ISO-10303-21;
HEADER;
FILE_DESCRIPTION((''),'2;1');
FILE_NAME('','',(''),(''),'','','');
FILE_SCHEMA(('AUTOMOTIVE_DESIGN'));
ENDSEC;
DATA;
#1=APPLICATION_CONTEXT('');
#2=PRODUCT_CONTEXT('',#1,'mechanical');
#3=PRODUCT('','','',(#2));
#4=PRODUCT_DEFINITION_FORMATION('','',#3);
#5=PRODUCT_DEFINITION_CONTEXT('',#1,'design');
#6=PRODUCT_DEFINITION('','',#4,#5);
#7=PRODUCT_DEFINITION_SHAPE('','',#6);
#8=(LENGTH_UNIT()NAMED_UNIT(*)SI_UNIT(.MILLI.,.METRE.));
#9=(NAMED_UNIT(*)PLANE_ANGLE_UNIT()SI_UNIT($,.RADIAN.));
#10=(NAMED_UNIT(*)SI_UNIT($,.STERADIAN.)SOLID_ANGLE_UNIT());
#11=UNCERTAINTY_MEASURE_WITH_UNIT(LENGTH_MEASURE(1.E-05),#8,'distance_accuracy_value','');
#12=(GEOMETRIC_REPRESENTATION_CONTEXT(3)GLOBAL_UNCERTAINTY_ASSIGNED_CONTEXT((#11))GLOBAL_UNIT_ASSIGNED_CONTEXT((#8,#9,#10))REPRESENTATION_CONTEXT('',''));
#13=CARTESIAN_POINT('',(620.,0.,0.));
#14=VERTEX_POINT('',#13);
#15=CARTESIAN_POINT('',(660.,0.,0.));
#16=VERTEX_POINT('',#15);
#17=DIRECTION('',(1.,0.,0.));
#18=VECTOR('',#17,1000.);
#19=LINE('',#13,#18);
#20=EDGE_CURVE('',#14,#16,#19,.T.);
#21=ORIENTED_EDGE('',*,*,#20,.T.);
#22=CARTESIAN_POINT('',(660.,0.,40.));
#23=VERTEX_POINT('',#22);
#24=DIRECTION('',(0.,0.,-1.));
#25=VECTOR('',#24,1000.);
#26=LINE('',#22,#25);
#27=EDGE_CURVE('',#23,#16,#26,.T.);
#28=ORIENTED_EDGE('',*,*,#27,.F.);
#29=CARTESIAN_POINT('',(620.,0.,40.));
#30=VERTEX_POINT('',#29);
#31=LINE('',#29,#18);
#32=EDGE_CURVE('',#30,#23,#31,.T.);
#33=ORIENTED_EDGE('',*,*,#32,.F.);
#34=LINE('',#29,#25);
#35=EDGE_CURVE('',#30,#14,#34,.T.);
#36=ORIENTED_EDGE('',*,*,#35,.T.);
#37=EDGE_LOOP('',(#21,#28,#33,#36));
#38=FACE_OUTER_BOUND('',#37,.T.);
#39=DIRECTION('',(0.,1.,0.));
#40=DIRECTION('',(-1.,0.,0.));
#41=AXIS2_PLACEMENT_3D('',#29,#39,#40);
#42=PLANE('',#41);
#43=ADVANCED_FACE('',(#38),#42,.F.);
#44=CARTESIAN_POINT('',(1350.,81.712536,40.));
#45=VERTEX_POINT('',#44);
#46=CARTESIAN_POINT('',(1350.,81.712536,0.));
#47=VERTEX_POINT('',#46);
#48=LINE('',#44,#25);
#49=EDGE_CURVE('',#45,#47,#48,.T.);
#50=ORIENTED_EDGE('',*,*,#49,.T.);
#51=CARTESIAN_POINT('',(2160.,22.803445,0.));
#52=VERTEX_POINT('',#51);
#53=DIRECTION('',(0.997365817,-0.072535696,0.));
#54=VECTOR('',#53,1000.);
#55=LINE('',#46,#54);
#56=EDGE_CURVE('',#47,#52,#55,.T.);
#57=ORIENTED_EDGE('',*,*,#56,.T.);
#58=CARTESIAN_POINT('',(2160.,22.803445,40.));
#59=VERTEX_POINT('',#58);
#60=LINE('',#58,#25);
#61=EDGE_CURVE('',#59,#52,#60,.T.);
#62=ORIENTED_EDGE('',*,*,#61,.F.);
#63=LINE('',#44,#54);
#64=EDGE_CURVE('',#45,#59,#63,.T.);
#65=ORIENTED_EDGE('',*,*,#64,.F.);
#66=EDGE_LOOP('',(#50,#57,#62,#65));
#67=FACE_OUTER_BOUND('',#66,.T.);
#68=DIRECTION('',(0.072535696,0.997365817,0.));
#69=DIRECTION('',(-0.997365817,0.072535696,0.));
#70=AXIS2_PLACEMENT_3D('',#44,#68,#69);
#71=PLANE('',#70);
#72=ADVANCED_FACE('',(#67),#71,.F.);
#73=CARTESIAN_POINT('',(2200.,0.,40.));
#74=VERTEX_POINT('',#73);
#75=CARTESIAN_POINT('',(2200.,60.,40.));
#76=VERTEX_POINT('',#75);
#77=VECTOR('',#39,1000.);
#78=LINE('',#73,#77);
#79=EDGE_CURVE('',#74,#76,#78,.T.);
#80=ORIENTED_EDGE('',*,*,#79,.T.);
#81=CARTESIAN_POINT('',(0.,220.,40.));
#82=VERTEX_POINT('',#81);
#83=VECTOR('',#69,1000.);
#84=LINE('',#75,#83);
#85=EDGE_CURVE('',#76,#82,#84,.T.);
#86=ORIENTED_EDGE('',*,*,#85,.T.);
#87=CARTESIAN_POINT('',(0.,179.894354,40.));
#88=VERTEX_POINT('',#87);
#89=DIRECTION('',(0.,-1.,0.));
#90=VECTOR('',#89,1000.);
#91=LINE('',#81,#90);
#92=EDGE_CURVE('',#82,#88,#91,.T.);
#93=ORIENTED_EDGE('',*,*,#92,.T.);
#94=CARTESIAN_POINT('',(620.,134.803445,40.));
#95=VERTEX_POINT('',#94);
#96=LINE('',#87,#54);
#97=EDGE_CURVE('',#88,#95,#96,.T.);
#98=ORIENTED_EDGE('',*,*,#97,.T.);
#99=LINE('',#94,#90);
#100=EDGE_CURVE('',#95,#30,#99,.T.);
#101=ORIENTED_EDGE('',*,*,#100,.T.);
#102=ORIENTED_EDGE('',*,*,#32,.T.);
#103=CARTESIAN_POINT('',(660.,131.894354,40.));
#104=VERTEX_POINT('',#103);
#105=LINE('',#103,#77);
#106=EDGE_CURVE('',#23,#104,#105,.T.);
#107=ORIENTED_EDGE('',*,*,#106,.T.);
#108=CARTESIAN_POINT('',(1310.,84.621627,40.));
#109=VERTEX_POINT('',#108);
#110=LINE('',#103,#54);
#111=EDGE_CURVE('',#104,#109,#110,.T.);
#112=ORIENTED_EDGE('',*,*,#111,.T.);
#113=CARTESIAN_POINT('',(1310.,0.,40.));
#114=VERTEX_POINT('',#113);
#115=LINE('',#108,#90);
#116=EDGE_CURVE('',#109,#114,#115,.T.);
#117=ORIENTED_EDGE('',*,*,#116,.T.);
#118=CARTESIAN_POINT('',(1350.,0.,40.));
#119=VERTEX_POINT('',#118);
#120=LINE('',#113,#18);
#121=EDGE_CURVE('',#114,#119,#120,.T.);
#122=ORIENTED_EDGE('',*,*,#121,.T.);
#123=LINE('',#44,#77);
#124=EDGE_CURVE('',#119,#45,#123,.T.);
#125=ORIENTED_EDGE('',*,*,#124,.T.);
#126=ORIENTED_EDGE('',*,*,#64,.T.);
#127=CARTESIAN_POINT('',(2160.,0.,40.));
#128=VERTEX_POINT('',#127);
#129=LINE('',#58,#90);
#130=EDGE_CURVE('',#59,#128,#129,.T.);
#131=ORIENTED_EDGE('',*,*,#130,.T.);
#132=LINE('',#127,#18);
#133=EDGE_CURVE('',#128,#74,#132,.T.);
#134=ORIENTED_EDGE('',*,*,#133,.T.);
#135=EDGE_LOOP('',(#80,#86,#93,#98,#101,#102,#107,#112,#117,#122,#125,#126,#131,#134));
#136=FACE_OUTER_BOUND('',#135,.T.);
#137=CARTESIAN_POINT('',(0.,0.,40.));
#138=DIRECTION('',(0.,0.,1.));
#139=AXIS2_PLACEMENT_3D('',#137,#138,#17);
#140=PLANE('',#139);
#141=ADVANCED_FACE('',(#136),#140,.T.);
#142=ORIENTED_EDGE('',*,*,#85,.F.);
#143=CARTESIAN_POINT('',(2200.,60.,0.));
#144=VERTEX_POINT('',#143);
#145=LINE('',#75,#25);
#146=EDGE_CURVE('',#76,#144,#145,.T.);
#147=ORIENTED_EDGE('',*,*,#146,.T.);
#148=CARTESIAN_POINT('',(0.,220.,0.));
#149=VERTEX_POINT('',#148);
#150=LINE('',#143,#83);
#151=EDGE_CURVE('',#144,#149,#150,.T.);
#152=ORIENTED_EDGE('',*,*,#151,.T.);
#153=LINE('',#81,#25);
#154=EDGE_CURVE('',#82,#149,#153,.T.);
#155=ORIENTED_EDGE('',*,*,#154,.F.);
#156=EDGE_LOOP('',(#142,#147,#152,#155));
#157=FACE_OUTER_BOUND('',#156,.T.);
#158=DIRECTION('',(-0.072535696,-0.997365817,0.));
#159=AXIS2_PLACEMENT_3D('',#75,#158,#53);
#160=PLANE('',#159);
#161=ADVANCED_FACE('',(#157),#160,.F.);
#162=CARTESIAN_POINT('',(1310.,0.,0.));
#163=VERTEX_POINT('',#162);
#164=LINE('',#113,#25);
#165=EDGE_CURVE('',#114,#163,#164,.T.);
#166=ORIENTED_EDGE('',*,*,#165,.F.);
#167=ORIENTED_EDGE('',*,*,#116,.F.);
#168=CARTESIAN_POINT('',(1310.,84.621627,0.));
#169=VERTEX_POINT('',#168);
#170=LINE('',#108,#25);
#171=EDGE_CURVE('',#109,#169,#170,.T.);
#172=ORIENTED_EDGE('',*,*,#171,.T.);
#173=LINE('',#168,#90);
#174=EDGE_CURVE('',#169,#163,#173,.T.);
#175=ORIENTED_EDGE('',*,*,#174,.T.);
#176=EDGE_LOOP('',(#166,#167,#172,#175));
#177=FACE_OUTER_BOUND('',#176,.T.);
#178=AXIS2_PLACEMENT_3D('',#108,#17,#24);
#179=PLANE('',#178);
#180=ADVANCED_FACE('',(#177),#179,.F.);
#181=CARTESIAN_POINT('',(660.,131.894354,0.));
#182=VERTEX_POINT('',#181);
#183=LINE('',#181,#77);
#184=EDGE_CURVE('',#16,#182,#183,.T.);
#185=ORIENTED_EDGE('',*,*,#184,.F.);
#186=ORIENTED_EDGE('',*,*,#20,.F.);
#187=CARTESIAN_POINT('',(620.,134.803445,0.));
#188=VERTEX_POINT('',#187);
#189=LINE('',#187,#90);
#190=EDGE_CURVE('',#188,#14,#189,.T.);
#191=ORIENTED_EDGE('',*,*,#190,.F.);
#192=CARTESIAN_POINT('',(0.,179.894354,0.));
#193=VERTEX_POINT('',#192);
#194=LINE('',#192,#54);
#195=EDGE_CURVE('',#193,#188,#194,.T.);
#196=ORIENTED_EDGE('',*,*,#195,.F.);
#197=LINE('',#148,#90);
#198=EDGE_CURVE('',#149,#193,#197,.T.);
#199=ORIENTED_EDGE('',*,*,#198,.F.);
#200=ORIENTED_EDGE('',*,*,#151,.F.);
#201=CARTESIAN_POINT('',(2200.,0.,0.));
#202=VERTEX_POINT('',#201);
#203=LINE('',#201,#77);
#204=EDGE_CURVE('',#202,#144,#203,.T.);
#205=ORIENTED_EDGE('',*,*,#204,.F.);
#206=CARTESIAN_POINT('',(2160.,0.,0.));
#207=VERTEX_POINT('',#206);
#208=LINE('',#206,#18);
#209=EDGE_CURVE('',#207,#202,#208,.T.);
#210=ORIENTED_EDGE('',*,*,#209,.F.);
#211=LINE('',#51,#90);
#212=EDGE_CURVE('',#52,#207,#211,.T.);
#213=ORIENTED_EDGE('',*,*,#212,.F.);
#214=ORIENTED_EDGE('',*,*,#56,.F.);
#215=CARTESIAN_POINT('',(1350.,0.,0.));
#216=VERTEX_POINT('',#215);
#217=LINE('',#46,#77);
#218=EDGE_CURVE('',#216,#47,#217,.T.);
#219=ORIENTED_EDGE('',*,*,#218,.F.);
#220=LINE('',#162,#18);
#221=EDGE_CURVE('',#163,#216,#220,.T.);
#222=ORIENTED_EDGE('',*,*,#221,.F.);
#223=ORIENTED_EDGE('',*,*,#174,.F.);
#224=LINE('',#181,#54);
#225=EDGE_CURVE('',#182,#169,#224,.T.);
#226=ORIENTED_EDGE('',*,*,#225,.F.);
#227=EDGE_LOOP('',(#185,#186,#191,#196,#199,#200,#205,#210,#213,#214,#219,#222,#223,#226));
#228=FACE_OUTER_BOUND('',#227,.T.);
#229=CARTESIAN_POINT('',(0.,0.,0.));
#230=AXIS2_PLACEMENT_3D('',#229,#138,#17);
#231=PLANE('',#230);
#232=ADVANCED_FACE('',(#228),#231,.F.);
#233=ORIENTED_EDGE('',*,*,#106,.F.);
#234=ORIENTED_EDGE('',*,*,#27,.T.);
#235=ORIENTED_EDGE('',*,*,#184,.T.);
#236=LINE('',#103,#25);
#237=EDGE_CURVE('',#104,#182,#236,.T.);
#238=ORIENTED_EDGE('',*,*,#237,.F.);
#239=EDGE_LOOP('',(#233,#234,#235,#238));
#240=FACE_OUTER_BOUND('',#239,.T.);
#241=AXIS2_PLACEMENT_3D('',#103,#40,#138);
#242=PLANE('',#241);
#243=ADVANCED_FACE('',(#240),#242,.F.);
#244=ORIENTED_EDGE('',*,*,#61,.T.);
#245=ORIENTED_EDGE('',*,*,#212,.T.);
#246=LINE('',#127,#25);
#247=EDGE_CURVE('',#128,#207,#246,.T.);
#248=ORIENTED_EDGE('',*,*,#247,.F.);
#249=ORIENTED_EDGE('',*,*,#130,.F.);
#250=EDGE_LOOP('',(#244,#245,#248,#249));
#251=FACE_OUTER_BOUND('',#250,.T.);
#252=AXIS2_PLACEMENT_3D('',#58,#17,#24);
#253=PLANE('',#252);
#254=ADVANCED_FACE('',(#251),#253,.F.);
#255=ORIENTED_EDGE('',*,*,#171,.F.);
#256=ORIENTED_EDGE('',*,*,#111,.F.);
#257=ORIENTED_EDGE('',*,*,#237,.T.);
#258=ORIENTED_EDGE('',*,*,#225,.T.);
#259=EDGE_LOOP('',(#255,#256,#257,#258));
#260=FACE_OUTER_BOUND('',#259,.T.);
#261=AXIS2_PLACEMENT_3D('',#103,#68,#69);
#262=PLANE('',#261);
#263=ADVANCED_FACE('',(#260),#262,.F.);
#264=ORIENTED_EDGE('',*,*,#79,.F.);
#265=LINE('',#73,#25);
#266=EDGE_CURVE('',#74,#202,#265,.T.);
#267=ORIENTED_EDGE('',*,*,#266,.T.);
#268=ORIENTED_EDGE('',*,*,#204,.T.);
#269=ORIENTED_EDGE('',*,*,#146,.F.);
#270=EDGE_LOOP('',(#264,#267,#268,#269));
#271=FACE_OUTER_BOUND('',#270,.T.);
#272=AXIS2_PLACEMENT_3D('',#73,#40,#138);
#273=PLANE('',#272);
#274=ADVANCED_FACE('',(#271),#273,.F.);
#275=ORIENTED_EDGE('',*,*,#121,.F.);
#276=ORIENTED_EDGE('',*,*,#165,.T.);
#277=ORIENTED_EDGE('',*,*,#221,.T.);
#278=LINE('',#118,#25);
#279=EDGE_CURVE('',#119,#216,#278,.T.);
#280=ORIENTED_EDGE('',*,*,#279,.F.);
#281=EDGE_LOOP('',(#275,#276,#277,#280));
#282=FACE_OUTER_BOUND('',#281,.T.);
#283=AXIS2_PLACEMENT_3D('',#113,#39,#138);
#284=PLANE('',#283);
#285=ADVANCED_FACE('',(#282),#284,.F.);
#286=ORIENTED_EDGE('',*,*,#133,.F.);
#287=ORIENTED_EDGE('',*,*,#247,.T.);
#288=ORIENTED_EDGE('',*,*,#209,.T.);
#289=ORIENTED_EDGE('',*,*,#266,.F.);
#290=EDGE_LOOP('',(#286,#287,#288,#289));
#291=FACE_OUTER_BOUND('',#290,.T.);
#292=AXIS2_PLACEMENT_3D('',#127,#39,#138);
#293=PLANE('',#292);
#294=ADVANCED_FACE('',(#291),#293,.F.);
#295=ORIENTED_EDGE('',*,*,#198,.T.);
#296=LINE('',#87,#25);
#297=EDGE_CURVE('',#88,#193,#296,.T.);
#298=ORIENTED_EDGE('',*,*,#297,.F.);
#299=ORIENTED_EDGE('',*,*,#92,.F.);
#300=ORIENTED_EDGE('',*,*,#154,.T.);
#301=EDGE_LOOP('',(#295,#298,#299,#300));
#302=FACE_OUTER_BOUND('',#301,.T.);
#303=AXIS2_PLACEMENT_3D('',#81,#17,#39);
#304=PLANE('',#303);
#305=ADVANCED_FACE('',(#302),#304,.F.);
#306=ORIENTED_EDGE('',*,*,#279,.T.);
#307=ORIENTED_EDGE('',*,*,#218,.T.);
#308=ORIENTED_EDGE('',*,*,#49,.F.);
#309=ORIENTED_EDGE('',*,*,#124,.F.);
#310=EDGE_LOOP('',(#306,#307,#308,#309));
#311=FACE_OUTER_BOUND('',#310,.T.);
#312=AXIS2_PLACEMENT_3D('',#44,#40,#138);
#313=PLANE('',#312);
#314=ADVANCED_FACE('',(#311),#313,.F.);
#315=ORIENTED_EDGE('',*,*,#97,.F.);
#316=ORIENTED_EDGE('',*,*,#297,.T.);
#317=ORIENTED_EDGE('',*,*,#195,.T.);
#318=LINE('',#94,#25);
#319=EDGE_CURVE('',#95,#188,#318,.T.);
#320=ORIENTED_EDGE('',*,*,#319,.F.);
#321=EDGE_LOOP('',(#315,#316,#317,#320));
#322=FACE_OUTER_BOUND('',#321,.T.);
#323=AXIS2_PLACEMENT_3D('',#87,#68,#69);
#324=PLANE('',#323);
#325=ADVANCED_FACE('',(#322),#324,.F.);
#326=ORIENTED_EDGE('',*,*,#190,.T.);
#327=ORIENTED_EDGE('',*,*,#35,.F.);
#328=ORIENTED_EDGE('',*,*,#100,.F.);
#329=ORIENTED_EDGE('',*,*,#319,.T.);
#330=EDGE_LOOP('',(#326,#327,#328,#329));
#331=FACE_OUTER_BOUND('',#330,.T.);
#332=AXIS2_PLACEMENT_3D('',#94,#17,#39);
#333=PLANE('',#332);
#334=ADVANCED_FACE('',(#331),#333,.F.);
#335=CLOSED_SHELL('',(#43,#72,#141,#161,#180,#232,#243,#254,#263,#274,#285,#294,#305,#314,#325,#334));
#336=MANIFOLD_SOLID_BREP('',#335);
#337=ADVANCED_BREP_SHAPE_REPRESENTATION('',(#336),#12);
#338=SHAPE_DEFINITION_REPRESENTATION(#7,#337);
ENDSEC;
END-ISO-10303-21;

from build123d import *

# Parameters (mm, degrees)
BOSS_EXTRUDE1_DEPTH = 40


with BuildPart() as part:
    # Sketch1 → Boss-Extrude1 (new body)
    with BuildSketch(Plane.XY):
        Polygon((2200, 0), (2200, 60), (0, 220), (0, 179.894354388), (620, 134.803445298), (620, 0), (660, 0), (660, 131.894354388), (1310, 84.621627116), (1310, 0), (1350, 0), (1350, 81.712536207), (2160, 22.803445298), (2160, 0), align=None)
    extrude(amount=BOSS_EXTRUDE1_DEPTH)


solid = part.part
